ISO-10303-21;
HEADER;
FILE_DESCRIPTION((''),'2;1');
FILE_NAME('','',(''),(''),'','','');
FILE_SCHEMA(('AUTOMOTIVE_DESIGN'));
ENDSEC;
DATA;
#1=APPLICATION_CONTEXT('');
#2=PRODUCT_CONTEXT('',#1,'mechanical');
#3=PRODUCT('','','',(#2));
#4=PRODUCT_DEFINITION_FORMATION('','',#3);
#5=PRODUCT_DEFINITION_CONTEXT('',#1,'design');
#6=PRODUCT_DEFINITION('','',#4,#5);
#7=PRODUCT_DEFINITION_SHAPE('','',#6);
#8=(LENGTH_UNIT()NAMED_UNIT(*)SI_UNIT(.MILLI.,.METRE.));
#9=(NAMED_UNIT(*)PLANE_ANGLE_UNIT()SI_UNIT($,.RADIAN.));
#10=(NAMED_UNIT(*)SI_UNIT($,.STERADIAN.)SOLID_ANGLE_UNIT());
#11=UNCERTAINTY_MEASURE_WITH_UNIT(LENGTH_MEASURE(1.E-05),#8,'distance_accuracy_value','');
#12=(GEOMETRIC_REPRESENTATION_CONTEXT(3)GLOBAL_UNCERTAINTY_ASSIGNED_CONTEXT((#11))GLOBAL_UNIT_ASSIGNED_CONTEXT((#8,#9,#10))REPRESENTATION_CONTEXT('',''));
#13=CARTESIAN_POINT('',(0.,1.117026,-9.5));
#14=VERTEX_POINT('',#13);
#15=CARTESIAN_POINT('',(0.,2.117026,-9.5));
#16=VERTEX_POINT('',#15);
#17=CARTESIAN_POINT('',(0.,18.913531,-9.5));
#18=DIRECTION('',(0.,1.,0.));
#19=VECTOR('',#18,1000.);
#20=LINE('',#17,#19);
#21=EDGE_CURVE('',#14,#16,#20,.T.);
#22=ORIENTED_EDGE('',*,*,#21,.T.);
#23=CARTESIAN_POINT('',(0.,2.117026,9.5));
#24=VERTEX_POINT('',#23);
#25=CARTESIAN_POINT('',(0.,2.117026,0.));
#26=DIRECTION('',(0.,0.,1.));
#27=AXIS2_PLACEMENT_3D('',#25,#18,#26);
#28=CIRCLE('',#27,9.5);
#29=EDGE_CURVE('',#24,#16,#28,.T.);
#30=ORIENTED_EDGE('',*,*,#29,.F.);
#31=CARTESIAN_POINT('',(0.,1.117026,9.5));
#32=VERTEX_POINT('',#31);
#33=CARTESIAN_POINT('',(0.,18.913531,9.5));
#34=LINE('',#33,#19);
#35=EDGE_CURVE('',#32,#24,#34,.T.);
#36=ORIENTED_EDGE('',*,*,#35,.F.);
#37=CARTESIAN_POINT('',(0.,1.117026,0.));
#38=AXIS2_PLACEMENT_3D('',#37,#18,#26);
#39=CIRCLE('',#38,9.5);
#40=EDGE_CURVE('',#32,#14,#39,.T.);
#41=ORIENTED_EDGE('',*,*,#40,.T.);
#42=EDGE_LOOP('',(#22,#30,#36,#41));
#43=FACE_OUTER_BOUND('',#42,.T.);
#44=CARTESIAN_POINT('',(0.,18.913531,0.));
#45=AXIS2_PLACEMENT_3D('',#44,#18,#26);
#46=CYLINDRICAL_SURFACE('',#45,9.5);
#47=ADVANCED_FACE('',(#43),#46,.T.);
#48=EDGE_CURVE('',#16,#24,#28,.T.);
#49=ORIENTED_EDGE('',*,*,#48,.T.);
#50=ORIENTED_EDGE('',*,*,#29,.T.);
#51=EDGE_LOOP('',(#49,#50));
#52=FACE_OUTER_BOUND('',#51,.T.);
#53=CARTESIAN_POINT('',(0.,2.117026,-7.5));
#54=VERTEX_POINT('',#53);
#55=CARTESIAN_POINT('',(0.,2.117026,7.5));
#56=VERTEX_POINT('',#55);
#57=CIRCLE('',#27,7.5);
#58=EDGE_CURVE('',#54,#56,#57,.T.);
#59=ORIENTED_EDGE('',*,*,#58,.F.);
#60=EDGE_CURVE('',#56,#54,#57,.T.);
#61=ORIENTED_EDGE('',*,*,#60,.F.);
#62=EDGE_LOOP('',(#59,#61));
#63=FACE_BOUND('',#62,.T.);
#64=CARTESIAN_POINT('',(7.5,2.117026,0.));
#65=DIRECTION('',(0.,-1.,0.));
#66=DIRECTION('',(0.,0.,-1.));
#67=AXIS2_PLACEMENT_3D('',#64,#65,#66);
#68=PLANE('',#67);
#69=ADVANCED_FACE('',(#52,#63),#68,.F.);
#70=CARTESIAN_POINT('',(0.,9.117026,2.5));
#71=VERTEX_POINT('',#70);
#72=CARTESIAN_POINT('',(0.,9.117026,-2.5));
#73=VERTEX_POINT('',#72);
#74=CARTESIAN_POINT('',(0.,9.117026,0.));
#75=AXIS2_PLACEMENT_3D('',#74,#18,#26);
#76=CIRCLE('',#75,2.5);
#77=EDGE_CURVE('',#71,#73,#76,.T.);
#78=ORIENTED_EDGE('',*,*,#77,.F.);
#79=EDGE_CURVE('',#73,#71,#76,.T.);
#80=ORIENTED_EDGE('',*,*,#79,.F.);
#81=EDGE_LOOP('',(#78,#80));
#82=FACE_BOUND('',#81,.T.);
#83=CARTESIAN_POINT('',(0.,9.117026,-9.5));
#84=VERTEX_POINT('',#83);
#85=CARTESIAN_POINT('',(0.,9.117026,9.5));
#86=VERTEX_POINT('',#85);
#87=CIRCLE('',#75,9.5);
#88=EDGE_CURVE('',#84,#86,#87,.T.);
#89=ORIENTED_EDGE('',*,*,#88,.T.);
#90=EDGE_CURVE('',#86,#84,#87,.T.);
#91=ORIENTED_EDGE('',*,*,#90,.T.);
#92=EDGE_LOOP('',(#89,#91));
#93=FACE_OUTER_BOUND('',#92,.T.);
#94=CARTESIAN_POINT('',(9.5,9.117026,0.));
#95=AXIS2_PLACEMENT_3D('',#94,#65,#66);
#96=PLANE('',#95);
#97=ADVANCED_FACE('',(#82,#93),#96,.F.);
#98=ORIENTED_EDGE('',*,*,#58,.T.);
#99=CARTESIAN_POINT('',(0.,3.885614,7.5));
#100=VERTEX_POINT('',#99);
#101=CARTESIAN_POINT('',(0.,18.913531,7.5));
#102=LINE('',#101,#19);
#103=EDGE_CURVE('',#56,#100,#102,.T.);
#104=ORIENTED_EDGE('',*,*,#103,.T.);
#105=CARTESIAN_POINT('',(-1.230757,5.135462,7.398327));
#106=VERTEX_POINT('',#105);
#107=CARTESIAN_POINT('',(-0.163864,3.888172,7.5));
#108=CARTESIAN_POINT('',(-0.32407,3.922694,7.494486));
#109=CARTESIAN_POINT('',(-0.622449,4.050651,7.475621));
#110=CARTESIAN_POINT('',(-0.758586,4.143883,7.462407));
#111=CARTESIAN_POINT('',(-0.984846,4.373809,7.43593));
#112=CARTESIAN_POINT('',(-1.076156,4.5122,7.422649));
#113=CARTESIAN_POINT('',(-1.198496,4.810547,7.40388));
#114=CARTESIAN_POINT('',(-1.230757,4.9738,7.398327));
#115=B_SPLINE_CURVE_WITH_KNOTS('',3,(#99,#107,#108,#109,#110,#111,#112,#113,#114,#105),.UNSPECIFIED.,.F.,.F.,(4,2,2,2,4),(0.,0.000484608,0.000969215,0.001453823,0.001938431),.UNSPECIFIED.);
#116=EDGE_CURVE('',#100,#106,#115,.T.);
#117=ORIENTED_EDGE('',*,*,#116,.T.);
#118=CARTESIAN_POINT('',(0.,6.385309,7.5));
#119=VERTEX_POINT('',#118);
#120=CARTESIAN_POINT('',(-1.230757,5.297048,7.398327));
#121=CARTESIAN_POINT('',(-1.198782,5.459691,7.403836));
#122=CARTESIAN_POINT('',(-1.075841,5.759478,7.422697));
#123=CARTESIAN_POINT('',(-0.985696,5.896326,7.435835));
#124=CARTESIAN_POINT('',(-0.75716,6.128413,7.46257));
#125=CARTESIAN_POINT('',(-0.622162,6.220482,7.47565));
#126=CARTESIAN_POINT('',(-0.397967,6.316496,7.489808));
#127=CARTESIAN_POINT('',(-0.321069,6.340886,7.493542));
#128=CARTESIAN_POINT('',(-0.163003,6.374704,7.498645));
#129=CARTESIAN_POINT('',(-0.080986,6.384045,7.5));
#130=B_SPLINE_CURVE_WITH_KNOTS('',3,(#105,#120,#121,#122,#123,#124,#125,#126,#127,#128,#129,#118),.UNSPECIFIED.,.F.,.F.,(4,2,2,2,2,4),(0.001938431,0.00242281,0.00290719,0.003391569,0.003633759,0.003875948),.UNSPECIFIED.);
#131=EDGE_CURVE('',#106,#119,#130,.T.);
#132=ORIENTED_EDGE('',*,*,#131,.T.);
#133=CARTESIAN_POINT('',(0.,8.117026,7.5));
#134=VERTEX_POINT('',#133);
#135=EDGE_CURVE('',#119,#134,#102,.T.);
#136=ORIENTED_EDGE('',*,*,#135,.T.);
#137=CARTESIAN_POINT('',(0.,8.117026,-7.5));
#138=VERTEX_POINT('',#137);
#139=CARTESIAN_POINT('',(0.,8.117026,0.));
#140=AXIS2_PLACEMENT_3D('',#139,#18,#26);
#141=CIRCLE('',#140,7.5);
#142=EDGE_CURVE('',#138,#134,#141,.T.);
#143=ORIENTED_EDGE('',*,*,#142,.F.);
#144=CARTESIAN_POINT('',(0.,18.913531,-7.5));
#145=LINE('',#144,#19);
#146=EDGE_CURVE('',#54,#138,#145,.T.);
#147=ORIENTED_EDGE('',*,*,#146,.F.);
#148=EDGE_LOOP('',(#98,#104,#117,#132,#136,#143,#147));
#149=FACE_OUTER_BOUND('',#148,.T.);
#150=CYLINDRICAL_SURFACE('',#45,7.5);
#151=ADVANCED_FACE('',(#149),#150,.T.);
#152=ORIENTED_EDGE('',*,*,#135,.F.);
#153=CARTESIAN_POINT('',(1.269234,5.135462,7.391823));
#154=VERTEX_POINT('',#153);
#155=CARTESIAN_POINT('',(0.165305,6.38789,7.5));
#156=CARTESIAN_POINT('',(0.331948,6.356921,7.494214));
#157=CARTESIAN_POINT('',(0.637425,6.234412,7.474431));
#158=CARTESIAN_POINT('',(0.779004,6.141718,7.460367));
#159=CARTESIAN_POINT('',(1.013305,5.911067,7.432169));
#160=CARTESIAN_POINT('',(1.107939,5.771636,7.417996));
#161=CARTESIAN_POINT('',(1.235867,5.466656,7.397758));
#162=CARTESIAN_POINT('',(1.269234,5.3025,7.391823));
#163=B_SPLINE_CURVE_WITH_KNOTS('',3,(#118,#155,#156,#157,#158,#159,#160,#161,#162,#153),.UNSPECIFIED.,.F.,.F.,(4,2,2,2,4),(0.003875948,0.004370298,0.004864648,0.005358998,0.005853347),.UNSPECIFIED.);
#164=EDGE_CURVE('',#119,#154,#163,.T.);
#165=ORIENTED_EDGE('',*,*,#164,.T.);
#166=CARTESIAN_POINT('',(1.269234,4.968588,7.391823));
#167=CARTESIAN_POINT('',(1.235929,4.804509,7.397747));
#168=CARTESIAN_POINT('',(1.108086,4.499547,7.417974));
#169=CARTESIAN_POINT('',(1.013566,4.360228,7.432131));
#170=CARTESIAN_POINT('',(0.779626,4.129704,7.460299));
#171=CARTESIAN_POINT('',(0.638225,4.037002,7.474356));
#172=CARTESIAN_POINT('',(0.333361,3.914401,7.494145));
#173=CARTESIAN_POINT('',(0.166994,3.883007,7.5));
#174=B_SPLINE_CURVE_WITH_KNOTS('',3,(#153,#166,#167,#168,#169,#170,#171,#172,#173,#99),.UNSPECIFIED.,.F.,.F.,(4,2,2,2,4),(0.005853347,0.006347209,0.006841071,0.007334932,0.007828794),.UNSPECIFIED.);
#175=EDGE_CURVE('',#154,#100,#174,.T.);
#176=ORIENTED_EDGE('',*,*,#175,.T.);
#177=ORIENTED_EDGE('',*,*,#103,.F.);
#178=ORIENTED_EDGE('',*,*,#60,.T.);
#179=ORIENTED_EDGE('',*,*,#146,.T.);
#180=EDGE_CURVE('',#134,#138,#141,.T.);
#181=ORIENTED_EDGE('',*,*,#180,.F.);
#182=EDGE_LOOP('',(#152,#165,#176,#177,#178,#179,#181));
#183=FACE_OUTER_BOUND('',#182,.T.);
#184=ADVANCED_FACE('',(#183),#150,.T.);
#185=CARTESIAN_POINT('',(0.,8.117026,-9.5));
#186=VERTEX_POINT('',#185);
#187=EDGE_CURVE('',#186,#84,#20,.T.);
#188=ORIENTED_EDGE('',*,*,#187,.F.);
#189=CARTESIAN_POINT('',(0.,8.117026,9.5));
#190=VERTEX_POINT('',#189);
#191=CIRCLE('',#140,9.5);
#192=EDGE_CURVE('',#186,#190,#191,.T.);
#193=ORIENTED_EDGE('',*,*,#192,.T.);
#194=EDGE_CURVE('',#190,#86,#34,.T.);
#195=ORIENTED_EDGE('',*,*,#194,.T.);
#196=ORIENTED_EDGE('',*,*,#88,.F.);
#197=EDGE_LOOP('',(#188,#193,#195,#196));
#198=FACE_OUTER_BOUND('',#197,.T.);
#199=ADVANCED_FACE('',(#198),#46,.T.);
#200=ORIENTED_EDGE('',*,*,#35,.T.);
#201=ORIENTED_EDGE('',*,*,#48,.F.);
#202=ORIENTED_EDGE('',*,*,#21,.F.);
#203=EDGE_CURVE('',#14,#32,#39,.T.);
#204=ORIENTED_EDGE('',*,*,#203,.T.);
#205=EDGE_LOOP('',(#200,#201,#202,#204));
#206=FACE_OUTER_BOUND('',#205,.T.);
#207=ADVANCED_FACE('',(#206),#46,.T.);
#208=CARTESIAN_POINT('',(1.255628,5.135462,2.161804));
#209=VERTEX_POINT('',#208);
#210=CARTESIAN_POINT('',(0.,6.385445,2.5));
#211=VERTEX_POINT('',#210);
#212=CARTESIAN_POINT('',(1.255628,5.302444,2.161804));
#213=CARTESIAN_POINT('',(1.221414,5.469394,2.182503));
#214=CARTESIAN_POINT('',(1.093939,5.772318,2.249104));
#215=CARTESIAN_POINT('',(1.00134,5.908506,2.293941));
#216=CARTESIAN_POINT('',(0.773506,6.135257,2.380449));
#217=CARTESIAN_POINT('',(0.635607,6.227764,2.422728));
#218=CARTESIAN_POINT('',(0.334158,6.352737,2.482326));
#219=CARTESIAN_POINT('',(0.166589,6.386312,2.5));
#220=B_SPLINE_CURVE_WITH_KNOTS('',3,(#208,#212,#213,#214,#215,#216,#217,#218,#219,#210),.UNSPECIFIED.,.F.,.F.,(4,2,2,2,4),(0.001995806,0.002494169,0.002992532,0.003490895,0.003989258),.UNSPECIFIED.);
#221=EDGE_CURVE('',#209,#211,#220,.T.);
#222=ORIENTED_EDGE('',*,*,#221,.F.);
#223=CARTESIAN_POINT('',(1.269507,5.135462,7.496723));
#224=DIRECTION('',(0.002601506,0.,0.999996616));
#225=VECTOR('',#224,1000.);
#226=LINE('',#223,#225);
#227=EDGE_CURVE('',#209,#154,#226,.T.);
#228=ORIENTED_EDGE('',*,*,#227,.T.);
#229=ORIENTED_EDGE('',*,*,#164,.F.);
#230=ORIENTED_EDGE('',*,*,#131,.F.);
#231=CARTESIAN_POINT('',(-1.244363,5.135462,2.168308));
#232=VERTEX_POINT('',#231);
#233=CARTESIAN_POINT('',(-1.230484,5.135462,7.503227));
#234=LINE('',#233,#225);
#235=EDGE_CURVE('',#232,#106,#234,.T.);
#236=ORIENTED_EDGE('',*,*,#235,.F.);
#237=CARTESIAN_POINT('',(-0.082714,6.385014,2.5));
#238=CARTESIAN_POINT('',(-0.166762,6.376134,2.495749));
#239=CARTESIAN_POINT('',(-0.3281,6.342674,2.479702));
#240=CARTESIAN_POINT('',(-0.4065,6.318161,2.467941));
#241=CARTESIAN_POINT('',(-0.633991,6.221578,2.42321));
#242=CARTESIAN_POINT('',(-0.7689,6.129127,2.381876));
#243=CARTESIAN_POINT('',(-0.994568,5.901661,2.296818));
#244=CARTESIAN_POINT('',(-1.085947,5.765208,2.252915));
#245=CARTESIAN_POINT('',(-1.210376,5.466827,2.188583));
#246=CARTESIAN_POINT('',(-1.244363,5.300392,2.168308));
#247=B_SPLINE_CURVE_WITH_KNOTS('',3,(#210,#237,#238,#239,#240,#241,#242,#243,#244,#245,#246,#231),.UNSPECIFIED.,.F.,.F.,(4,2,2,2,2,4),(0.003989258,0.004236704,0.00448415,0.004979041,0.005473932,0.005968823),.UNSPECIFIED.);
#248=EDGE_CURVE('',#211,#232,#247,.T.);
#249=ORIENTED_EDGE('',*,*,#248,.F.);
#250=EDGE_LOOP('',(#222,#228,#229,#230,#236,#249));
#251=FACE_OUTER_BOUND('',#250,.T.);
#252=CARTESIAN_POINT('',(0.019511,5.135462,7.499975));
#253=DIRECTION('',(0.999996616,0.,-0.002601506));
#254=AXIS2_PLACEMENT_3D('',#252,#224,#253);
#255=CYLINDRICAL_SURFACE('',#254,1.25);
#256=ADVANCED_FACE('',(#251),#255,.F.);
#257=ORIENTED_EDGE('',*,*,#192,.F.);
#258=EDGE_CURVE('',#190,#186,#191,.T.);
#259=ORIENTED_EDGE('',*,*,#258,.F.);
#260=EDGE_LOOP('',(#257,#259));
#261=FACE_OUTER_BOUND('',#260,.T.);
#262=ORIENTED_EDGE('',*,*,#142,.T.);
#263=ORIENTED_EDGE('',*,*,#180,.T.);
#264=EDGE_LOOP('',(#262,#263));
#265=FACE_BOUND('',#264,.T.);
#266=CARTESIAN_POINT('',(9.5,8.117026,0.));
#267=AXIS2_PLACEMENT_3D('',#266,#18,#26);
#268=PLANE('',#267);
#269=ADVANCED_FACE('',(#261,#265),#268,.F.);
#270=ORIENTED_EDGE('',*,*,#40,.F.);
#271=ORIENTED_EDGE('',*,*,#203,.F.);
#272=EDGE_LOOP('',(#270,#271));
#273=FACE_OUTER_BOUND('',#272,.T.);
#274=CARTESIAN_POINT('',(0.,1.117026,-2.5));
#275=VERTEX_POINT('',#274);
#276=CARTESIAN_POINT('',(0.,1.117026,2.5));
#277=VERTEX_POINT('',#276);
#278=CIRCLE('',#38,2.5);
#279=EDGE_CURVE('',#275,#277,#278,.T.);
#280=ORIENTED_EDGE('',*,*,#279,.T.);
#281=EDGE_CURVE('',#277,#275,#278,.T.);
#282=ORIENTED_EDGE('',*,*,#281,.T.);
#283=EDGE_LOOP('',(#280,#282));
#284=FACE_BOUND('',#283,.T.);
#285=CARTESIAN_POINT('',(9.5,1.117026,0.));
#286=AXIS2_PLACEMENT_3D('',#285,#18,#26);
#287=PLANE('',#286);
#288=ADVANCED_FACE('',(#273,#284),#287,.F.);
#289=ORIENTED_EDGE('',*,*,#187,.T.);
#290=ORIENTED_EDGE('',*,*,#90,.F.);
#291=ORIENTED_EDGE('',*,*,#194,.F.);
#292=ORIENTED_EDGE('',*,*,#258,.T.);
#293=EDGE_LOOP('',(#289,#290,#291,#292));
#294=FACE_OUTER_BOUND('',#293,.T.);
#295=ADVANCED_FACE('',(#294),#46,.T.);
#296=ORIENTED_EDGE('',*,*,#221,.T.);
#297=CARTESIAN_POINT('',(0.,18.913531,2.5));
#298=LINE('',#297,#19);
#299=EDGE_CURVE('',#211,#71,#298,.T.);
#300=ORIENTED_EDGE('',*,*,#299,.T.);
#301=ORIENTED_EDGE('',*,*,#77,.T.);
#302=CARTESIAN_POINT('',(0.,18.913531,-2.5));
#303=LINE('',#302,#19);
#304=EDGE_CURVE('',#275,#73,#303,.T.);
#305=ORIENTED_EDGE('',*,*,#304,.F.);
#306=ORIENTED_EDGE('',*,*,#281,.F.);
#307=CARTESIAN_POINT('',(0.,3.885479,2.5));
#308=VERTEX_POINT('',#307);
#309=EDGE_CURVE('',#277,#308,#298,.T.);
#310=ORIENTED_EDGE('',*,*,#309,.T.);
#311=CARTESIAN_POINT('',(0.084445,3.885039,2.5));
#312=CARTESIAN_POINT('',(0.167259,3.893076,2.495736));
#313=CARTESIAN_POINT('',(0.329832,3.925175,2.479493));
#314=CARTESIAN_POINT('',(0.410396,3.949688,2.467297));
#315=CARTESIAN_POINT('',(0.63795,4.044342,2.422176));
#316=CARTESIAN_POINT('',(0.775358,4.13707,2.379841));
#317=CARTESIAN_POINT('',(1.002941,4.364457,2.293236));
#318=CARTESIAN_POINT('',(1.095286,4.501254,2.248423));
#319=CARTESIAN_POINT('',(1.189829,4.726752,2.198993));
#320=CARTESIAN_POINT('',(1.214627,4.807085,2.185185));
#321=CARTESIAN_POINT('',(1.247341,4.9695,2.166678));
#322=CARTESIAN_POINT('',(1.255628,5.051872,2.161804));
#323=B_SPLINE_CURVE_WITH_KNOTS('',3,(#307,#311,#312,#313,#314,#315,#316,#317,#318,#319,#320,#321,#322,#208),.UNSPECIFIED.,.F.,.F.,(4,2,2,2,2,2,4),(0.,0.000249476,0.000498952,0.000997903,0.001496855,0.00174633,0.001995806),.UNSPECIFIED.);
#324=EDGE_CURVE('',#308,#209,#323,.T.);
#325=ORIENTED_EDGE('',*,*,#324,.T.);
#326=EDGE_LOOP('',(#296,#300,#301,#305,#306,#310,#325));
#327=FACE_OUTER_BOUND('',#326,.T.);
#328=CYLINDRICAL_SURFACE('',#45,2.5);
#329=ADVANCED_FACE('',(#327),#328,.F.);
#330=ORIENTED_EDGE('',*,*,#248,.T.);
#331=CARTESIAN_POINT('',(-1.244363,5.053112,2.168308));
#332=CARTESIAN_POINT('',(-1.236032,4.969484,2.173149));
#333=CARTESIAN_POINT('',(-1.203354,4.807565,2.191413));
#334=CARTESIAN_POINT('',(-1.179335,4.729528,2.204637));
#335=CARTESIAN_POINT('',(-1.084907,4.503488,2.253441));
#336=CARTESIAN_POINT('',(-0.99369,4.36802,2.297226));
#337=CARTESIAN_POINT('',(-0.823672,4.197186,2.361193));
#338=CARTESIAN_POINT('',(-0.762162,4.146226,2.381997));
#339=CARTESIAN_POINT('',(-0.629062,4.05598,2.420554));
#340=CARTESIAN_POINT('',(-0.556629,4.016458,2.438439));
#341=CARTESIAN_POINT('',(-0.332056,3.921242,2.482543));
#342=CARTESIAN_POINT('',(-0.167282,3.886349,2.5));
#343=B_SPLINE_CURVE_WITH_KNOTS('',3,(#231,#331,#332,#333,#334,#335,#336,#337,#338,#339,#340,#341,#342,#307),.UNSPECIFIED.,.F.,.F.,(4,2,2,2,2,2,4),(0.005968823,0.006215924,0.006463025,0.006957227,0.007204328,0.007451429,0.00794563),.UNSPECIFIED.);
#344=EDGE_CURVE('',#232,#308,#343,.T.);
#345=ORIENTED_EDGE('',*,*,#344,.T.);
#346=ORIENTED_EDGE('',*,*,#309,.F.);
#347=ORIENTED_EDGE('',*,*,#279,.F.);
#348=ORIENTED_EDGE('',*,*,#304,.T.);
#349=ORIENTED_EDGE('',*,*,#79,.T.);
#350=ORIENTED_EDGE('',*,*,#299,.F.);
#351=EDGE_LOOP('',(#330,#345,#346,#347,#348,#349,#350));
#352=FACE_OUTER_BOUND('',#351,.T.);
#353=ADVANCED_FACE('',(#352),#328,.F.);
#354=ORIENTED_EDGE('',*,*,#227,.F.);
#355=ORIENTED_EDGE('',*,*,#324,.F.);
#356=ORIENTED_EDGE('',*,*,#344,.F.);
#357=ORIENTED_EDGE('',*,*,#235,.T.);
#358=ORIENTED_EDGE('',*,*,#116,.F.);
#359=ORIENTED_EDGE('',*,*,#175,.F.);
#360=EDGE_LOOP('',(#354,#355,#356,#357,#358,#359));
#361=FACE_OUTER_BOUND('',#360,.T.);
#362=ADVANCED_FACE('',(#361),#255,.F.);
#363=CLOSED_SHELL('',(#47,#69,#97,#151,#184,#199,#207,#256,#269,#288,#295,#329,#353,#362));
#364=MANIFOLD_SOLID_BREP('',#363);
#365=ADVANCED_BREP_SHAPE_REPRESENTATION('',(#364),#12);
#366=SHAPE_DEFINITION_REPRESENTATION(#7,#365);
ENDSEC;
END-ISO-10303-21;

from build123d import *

# Parameters (mm, degrees)
HOLE_WIZARD_M3_1_REACH  = 21.894
HOLE_WIZARD_M3_1_BORE_R = 1.25


with BuildPart() as part:
    # 草图1 → 旋转1 (revolve)
    with BuildSketch(Plane.XY, mode=Mode.PRIVATE) as revolve_1_sk:
        Polygon((9.5, 9.117025796), (2.5, 9.117025796), (2.5, 1.117025796), (9.5, 1.117025796), (9.5, 2.117025796), (7.5, 2.117025796), (7.5, 8.117025796), (9.5, 8.117025796), align=None)
    revolve(revolve_1_sk.sketch.rotate(Axis((0, 18.913531016, 0), (0, -1, 0)), 90), axis=Axis((0, 18.913531016, 0), (0, -1, 0)))

    # M3 螺纹孔1 bore (on position points) → M3 螺纹孔1 (cut, up to next)
    with BuildSketch(Plane(origin=(0.019511296, 5.135461688, 7.499974621), x_dir=(0.999996616077, 0, -0.002601506145), z_dir=(0.002601506145, 0, 0.999996616077)), mode=Mode.PRIVATE) as hole_wizard_m3_1_sk1:
        Circle(HOLE_WIZARD_M3_1_BORE_R)
    hole_wizard_m3_1_tool1 = extrude(hole_wizard_m3_1_sk1.sketch, amount=-HOLE_WIZARD_M3_1_REACH, mode=Mode.PRIVATE) & part.part
    add(hole_wizard_m3_1_tool1.solids().sort_by_distance((0.019511, 5.135462, 7.499975))[0], mode=Mode.SUBTRACT)


solid = part.part
